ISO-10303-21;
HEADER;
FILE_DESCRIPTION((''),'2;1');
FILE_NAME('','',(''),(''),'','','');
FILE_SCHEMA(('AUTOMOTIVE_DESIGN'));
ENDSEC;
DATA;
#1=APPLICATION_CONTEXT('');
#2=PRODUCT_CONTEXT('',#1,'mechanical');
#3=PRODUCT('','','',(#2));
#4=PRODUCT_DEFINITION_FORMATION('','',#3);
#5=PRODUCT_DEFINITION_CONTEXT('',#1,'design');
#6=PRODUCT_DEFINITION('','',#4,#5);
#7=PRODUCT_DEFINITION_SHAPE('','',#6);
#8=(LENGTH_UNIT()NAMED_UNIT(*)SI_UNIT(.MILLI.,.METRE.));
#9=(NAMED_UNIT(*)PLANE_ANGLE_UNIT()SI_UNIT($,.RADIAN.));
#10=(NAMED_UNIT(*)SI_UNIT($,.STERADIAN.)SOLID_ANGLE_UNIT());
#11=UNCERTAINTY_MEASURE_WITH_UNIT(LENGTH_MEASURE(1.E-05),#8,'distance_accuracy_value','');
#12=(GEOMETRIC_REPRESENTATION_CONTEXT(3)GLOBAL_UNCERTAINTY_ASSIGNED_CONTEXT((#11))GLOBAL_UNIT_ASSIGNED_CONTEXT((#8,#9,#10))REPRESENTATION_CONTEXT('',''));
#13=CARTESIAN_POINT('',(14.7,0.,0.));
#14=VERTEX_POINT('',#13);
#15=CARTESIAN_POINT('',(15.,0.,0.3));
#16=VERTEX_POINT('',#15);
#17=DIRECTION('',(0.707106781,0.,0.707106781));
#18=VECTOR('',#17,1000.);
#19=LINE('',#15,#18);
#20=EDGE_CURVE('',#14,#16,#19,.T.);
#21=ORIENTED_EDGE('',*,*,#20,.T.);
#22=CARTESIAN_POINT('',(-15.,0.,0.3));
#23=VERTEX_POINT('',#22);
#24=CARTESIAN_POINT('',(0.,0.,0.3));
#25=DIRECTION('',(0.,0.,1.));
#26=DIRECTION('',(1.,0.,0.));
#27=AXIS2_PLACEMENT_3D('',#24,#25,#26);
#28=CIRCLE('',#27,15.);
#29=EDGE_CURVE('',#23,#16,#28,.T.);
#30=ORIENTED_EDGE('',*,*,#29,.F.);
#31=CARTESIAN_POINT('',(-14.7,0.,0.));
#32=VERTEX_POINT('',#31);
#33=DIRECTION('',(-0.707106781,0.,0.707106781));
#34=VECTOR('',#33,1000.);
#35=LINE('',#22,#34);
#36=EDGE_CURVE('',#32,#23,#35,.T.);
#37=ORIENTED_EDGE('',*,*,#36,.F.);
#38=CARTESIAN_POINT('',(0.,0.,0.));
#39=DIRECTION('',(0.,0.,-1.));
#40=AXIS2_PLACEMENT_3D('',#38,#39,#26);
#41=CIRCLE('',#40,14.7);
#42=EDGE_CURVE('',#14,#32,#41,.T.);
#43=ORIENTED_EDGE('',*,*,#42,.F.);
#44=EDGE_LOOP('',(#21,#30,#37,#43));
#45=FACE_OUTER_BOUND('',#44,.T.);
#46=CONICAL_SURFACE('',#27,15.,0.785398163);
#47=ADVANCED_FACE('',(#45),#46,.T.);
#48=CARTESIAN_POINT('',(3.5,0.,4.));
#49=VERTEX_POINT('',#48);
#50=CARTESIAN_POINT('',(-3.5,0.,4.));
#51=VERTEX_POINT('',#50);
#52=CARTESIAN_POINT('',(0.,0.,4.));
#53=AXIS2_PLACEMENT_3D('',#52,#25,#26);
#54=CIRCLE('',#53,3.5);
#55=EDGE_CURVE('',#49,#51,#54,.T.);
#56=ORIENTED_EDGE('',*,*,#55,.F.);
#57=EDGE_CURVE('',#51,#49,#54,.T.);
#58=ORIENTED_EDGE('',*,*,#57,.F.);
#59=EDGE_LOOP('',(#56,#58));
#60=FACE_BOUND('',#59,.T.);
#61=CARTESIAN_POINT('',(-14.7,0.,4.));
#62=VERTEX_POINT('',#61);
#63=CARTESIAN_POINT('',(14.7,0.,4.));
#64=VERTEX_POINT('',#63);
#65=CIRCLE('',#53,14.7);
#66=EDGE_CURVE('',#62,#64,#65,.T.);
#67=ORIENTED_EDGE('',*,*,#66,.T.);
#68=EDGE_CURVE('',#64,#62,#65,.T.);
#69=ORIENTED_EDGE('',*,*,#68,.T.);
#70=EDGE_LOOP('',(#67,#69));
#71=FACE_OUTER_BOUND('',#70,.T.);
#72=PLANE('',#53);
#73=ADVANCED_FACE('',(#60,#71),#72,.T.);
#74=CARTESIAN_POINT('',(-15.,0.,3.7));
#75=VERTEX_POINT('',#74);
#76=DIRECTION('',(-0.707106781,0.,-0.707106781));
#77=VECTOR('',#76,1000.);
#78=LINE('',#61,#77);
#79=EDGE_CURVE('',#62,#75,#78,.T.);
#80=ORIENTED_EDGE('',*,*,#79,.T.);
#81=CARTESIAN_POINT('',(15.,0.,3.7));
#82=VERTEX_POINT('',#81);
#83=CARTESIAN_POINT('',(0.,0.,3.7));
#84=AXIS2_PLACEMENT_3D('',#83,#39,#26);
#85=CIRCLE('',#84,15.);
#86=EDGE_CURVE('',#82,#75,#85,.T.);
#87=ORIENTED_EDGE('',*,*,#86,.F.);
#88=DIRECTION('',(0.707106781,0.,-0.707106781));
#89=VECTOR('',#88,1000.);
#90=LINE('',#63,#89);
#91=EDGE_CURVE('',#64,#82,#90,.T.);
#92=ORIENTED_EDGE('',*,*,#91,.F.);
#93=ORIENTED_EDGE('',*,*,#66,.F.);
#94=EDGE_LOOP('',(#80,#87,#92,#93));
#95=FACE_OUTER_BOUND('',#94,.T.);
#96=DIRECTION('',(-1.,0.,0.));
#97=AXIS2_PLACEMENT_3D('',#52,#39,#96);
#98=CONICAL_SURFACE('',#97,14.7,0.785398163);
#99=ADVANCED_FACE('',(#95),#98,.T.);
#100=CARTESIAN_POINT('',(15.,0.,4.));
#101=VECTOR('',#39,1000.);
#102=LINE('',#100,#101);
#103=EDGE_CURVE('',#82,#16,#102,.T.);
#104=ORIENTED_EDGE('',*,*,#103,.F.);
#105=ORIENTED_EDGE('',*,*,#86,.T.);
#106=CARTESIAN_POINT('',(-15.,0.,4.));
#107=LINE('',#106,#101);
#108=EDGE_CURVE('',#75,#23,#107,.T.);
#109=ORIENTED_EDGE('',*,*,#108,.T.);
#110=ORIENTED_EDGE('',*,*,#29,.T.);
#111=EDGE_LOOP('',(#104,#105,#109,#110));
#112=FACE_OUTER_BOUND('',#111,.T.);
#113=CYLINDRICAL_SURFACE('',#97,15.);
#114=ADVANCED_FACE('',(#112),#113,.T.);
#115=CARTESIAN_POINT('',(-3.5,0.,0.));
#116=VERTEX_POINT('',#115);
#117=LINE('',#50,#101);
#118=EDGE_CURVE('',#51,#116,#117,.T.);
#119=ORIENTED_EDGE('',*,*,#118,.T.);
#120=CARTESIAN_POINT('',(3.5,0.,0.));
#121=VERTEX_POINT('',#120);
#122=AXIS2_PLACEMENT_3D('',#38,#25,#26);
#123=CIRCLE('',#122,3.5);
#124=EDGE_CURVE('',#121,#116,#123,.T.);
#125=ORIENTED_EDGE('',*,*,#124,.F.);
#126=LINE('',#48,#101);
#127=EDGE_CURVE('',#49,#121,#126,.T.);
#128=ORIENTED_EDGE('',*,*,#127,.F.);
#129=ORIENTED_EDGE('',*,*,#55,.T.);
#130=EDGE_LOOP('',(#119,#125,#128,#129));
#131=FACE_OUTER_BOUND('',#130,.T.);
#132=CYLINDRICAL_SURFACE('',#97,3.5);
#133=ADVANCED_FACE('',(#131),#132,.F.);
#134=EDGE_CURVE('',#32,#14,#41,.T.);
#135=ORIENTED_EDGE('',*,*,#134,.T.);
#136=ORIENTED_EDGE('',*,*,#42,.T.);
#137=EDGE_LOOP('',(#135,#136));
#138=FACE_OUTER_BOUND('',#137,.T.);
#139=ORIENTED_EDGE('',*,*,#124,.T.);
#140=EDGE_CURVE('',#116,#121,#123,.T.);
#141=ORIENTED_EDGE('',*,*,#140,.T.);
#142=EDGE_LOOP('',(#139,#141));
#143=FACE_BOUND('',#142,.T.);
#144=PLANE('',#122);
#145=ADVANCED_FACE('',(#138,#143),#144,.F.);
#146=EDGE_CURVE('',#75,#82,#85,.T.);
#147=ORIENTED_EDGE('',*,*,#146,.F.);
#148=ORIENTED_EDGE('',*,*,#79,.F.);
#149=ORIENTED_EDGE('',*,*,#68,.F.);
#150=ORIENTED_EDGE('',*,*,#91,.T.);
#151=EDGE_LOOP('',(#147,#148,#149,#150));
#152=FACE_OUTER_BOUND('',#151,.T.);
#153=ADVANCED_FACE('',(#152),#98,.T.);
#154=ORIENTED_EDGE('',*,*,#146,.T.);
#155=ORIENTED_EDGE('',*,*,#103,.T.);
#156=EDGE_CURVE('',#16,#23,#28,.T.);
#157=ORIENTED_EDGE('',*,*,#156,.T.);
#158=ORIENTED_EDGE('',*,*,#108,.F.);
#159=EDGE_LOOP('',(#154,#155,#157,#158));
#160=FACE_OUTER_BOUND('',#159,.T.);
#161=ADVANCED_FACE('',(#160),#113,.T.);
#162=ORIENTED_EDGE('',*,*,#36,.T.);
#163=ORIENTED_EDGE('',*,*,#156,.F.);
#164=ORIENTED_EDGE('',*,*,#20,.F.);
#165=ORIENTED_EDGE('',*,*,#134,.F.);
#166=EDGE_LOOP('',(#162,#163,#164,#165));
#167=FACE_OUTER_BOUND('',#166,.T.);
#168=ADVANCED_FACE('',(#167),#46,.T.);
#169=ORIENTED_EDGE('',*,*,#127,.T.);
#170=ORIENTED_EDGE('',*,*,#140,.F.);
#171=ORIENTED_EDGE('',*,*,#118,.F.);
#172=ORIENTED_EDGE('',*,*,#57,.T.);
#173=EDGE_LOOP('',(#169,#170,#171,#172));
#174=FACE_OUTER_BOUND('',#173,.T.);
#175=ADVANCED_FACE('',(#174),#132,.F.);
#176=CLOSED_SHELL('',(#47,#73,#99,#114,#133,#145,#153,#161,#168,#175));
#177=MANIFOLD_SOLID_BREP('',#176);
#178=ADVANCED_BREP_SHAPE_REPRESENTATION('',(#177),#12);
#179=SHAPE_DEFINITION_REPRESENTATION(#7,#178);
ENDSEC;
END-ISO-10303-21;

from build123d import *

# Parameters (mm, degrees)
SKETCH1_R           = 15
SKETCH1_R_2         = 3.5
BOSS_EXTRUDE1_DEPTH = 4
CHAMFER1_SIZE       = 0.3


with BuildPart() as part:
    # Sketch1 → Boss-Extrude1 (new body)
    with BuildSketch(Plane.XY):
        Circle(SKETCH1_R)
        Circle(SKETCH1_R_2, mode=Mode.SUBTRACT)
    extrude(amount=BOSS_EXTRUDE1_DEPTH)

    # Chamfer1
    chamfer1_edges = [part.edges().sort_by_distance(p)[0] for p in [
        (-15, 0, 0),
        (-15, 0, 4),
    ]]
    chamfer(chamfer1_edges, length=CHAMFER1_SIZE)


solid = part.part
